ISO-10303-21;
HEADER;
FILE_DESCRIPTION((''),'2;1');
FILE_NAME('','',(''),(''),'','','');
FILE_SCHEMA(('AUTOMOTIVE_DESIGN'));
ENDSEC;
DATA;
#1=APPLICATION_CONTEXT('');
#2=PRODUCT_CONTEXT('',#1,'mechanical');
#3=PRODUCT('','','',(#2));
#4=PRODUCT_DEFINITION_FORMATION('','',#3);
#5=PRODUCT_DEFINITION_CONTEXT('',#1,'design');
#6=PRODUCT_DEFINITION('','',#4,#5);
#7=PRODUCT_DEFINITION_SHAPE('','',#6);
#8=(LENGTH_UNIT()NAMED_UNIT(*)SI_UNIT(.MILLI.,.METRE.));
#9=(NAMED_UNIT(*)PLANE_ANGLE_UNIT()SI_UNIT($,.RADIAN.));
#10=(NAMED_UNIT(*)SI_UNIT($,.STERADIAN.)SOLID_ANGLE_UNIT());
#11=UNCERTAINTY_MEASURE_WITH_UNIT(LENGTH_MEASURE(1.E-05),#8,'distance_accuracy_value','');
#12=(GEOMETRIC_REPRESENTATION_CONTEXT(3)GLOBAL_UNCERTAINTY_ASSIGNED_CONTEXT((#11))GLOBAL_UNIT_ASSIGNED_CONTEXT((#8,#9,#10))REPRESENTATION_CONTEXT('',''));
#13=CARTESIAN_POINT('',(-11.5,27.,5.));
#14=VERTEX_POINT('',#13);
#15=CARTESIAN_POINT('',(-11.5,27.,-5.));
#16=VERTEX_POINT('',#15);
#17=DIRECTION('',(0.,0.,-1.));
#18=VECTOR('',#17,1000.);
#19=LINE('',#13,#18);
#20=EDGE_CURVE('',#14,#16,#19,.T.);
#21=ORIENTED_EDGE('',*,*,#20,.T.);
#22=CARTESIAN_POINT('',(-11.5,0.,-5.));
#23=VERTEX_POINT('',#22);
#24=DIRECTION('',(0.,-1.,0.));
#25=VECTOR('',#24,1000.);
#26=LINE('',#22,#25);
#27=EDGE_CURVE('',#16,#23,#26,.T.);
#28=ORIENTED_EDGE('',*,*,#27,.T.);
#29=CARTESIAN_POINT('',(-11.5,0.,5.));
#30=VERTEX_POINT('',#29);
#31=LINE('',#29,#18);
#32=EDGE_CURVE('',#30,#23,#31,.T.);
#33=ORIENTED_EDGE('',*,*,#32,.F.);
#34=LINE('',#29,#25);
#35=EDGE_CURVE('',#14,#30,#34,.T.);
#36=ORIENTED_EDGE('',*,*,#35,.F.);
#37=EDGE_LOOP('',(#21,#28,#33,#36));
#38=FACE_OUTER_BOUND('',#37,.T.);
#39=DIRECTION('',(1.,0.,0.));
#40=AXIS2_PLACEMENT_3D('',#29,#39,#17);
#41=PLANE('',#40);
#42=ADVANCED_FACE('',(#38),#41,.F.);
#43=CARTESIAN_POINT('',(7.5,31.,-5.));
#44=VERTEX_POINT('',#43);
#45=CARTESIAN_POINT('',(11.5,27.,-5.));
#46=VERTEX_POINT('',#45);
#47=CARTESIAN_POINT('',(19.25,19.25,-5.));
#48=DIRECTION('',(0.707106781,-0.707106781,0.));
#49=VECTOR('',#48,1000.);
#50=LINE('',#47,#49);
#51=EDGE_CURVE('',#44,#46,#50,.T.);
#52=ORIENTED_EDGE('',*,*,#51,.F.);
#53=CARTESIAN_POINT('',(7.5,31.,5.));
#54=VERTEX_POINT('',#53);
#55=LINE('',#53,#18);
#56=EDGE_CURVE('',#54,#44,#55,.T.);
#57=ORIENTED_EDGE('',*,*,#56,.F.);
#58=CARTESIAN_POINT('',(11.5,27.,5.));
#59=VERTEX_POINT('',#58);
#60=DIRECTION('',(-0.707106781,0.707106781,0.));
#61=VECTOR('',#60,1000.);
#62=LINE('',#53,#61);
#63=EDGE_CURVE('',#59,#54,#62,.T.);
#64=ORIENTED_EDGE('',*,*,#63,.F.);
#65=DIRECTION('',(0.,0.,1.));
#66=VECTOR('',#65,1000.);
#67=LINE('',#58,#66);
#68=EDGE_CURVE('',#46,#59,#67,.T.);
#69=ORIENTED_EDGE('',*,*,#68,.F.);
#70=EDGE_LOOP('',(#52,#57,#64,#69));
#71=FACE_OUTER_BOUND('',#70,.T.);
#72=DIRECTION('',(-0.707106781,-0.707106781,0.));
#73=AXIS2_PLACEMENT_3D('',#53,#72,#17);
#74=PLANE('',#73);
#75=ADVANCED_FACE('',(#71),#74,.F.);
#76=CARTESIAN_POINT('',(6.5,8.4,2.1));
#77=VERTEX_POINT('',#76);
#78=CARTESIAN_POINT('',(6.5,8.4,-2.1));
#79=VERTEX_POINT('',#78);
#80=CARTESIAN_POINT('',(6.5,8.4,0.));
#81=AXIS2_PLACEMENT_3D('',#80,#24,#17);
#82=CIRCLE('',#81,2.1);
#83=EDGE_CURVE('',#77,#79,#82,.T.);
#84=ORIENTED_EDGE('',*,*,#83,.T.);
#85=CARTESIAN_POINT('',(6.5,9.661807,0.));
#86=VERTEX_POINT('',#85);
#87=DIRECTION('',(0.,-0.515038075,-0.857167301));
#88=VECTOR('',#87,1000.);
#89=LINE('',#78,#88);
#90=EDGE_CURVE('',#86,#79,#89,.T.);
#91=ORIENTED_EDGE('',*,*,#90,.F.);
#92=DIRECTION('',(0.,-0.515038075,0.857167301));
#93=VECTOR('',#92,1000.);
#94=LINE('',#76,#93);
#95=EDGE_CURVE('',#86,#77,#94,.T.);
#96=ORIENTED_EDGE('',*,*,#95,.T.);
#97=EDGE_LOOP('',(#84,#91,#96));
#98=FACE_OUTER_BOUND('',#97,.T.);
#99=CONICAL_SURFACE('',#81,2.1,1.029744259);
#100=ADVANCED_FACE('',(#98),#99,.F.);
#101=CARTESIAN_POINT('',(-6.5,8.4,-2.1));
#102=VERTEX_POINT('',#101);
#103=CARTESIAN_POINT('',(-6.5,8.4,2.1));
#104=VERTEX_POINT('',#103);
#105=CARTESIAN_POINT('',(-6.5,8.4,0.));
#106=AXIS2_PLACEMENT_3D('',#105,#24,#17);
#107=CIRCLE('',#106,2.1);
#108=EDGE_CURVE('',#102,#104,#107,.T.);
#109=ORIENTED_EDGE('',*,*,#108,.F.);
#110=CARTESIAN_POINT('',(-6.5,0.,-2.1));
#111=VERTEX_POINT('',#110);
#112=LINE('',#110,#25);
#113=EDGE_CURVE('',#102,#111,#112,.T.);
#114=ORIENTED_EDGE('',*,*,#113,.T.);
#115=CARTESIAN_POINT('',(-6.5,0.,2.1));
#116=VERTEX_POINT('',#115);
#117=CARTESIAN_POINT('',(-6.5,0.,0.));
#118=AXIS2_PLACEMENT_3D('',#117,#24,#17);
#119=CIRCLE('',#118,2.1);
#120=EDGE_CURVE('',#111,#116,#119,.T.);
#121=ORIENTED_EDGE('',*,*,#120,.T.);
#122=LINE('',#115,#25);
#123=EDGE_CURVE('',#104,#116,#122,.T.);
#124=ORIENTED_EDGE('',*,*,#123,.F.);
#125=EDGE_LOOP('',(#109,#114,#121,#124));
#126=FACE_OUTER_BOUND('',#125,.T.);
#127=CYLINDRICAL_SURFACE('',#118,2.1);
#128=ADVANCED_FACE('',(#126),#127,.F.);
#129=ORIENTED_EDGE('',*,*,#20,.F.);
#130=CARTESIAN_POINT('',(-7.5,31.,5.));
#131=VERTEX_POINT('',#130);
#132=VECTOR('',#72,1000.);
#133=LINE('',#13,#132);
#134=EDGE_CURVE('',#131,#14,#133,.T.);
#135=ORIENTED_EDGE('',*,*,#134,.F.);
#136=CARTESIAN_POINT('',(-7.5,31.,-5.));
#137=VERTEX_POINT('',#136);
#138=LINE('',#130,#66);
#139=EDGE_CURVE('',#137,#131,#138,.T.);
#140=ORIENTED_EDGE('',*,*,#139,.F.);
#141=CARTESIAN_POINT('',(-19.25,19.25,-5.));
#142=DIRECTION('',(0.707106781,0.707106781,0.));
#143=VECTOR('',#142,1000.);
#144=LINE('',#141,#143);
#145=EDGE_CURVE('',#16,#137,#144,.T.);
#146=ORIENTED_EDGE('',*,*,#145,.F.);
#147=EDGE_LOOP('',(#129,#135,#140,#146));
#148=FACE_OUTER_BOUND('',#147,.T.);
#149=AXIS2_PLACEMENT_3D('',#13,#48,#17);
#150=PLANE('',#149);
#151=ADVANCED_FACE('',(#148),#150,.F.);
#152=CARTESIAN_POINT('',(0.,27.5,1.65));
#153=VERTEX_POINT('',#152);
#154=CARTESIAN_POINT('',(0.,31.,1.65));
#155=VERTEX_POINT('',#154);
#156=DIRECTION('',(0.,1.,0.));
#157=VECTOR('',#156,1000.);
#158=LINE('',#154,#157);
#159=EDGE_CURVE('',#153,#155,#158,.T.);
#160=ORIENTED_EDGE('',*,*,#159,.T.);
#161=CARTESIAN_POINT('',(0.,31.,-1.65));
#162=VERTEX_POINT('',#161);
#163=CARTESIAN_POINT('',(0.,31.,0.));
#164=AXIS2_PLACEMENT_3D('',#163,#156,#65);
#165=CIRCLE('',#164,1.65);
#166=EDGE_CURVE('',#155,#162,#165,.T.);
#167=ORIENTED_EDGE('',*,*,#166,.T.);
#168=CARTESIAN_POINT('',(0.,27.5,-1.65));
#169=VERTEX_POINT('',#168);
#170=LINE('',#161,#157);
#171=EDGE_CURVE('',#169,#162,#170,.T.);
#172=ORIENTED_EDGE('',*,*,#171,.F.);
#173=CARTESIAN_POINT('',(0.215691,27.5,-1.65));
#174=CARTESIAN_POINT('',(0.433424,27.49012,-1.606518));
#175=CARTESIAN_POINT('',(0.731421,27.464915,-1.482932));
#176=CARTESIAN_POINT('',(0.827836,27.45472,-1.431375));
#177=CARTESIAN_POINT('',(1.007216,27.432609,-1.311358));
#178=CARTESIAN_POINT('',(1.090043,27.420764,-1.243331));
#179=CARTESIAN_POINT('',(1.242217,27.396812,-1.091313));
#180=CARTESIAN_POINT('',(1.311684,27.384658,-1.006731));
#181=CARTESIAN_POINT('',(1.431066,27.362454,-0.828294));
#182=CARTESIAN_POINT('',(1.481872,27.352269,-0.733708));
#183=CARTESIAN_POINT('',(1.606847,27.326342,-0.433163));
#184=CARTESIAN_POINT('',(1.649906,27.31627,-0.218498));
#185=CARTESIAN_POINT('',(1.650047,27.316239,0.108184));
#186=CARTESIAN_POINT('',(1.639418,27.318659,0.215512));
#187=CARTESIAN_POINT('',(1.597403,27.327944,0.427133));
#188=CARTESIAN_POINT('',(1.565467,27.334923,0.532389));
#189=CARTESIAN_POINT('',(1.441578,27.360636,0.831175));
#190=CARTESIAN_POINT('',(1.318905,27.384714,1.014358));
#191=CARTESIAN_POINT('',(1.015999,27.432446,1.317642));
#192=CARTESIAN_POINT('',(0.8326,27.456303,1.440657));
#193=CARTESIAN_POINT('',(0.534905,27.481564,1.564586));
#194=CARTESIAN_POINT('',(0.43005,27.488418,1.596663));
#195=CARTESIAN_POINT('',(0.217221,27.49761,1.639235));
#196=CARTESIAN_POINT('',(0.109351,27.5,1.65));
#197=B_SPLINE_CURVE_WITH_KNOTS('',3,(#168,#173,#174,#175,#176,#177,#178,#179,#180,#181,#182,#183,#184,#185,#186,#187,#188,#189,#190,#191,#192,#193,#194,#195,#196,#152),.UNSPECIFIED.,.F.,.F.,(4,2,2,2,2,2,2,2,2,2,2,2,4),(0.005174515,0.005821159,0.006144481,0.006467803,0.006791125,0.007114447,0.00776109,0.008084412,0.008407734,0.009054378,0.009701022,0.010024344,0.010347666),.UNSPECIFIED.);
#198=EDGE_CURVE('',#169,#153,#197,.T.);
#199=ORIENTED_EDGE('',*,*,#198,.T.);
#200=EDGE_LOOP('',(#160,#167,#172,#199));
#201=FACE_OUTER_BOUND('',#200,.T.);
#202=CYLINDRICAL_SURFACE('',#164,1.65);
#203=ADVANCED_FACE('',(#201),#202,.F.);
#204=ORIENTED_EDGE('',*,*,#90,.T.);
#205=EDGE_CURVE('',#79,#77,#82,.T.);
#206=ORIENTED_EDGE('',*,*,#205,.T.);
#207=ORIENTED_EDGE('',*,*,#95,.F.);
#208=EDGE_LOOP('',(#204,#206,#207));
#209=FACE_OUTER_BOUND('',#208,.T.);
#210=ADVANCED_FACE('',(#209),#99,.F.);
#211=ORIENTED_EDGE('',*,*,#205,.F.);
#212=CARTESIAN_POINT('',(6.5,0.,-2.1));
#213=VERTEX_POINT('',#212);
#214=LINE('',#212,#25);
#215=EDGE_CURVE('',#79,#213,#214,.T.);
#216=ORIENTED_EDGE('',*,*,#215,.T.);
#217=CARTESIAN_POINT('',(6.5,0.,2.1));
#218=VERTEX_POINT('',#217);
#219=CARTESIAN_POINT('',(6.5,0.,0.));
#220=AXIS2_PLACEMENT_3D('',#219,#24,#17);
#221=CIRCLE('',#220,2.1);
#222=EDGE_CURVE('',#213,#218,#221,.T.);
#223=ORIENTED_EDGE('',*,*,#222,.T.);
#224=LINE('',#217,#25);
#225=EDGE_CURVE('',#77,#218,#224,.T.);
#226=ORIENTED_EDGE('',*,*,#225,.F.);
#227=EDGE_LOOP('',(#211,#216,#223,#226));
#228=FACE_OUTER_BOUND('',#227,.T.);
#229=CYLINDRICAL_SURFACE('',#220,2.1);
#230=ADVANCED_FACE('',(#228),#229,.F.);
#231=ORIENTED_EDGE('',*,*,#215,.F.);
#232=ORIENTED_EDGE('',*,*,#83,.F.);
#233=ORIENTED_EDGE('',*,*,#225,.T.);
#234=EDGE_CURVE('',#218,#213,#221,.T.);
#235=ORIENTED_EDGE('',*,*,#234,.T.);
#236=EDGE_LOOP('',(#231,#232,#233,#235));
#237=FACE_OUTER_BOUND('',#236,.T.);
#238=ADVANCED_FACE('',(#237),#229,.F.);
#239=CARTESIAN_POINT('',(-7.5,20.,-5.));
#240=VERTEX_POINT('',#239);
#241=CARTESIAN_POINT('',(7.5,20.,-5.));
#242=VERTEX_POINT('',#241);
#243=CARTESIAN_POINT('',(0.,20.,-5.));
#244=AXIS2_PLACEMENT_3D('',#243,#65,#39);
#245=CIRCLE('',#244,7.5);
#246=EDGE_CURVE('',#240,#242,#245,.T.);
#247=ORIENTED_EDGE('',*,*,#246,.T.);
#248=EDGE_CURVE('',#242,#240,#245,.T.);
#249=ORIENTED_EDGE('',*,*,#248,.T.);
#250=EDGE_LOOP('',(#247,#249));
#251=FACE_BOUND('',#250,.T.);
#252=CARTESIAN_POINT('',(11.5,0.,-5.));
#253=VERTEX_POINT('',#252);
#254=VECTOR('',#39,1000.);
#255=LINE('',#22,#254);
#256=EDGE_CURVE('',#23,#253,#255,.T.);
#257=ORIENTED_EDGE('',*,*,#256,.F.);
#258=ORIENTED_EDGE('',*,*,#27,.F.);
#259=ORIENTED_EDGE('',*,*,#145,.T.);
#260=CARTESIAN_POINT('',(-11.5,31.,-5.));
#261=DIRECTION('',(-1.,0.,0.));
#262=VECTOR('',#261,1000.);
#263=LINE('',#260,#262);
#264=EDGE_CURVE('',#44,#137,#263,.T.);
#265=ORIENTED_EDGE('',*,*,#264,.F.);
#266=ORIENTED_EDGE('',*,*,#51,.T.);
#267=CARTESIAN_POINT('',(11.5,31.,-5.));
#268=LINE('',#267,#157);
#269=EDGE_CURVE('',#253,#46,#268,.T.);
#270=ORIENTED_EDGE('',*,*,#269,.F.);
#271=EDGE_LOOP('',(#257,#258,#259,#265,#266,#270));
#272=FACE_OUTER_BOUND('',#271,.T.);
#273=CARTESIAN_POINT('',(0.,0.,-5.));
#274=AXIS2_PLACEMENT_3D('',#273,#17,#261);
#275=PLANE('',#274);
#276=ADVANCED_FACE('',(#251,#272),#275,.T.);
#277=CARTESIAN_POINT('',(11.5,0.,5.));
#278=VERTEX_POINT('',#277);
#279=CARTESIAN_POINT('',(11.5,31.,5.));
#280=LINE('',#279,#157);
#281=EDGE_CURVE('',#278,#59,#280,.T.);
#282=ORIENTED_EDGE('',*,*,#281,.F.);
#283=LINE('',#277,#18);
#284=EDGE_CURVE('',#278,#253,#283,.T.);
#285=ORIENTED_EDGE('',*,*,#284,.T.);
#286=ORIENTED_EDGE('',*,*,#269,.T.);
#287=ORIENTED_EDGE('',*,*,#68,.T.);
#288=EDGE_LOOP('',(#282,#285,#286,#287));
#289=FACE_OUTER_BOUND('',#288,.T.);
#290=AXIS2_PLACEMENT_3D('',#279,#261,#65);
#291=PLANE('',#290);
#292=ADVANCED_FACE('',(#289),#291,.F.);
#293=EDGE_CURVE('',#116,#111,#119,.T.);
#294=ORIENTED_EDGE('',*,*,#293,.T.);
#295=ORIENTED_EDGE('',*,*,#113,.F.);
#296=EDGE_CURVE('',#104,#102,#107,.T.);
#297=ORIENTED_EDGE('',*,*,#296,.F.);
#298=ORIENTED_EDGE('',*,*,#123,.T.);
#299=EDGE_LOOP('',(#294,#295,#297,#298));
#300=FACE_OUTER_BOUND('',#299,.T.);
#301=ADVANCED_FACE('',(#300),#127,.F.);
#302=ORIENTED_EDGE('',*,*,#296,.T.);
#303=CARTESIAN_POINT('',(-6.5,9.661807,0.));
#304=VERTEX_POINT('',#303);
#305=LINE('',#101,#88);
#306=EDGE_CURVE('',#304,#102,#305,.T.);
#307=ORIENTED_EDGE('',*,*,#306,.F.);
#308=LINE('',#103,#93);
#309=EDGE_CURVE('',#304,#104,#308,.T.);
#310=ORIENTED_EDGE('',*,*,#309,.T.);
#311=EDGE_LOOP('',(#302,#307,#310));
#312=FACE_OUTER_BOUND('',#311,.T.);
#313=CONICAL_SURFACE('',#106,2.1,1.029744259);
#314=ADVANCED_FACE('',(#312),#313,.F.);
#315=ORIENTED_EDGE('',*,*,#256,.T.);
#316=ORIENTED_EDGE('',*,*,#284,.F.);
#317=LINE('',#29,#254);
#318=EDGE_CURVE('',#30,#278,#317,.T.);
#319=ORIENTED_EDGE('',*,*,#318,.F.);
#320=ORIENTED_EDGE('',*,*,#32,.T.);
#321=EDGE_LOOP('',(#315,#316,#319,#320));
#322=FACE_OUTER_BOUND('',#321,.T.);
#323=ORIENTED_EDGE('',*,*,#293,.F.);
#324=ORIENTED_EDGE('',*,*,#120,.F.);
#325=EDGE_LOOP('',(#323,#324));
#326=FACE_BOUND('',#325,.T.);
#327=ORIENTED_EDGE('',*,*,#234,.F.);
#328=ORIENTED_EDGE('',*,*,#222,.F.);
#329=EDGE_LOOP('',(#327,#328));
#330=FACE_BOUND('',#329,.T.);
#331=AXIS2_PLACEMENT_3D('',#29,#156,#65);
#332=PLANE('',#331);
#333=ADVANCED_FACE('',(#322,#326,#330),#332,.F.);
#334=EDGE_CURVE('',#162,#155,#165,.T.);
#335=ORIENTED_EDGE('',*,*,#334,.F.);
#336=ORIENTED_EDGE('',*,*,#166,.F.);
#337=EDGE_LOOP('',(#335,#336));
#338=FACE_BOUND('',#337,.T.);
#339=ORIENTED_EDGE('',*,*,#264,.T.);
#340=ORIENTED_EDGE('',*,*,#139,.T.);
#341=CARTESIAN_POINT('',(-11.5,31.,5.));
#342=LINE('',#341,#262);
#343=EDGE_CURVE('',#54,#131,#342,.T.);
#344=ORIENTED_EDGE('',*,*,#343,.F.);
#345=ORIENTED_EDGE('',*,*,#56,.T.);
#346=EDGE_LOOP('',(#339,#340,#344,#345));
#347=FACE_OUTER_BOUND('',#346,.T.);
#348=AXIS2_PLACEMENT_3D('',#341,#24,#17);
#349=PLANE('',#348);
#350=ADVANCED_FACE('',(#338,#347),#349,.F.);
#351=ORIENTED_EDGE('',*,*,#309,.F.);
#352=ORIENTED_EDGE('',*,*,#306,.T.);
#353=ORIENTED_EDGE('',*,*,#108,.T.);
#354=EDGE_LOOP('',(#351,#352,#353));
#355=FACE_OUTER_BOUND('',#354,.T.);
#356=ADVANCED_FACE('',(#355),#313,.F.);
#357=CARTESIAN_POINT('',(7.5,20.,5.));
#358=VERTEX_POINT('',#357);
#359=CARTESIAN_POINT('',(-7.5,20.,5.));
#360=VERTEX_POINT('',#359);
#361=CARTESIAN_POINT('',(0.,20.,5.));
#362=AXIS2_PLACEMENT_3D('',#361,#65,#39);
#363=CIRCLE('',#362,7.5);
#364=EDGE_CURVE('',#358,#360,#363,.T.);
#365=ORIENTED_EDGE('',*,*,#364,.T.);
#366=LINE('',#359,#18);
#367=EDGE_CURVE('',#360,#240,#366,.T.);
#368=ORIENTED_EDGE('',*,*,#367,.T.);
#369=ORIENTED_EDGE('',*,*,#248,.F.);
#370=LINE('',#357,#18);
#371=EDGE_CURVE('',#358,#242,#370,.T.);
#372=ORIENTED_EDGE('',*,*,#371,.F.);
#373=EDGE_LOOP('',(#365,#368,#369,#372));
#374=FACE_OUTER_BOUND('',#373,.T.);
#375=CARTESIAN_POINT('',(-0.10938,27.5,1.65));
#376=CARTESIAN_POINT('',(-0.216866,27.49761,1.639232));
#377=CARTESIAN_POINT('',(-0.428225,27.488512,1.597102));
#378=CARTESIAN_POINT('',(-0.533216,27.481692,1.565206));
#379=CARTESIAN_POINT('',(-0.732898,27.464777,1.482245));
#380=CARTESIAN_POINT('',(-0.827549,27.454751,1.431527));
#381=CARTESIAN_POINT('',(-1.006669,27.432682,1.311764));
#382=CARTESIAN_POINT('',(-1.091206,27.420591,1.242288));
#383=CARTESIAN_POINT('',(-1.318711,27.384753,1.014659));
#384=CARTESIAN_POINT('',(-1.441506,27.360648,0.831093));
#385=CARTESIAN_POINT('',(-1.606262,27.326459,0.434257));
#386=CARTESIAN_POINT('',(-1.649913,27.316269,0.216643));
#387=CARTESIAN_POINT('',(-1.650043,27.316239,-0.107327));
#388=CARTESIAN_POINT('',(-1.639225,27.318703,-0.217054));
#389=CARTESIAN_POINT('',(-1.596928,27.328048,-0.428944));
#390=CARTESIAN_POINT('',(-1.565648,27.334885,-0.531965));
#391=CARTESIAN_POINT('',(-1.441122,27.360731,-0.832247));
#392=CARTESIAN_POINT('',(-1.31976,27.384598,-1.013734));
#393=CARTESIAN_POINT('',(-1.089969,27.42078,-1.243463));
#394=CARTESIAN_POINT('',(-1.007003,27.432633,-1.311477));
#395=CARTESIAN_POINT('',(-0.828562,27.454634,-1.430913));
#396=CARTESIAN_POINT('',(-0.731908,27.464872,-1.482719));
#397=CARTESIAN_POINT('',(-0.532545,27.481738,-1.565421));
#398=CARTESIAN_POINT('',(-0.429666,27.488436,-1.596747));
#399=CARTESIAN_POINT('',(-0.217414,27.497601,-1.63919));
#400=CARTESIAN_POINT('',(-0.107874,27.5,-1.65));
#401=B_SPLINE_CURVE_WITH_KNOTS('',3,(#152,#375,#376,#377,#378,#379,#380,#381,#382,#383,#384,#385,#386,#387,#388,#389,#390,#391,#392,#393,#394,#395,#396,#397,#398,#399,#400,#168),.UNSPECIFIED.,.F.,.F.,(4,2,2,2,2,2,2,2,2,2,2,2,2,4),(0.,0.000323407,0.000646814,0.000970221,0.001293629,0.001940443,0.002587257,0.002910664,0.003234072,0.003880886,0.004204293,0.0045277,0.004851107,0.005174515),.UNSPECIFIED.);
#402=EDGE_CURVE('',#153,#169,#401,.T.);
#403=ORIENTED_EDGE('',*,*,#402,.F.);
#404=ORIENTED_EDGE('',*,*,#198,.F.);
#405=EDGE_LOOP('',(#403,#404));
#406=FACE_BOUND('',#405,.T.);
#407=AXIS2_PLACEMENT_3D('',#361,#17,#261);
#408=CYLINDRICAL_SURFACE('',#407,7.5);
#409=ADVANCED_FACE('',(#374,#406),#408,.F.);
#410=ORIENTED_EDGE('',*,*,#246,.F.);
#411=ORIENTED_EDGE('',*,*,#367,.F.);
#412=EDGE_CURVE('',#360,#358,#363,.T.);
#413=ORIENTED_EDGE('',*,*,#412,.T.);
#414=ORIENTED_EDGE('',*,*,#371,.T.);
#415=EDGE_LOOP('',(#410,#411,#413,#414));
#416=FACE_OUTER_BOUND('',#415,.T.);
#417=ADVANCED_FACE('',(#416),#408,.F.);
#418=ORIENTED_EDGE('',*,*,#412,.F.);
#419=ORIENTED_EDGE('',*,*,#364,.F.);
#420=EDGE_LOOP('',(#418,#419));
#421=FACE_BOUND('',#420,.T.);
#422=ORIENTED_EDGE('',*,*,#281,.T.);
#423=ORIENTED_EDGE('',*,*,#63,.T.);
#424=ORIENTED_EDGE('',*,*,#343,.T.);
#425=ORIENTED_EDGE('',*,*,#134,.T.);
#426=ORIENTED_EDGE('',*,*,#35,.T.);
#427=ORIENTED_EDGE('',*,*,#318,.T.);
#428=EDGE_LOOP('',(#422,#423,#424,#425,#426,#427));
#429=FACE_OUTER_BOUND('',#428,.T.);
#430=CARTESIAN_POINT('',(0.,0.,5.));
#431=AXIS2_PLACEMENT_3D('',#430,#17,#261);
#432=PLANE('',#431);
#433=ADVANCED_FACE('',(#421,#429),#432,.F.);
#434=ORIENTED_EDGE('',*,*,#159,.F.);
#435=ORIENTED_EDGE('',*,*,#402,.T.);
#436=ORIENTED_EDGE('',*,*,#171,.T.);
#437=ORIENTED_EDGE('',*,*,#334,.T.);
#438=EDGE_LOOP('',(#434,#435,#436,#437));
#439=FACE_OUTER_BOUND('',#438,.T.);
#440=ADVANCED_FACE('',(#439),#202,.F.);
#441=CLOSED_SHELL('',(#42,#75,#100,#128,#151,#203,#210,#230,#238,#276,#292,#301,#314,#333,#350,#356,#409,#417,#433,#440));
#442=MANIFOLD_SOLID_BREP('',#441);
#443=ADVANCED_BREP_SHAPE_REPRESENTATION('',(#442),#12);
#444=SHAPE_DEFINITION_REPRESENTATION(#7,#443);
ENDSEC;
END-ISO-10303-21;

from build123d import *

# Parameters (mm, degrees)
SKETCH_1_W              = 23
SKETCH_1_H              = 31
SKETCH_1_R              = 7.5
EXTRUDE_1_DEPTH         = 5
CHAMFER_1_SIZE          = 4
HOLE_WIZARD_M4_1_REACH  = 35.44
HOLE_WIZARD_M4_1_BORE_R = 1.65
HOLE_WIZARD_M5_2_D      = 4.2
HOLE_WIZARD_M5_2_DEPTH  = 8.4
HOLE_WIZARD_M5_2_TIP    = 1.2618073


with BuildPart() as part:
    # 草图1 → 凸台-拉伸1 (new, symmetric)
    with BuildSketch(Plane.XY):
        with Locations((0, 15.5)):
            Rectangle(SKETCH_1_W, SKETCH_1_H)
        with Locations((0, 20)):
            Circle(SKETCH_1_R, mode=Mode.SUBTRACT)
    extrude(amount=EXTRUDE_1_DEPTH, both=True)

    # 倒角1
    chamfer_1_edges = [part.edges().sort_by_distance(p)[0] for p in [
        (11.5, 31, 0),
        (-11.5, 31, 0),
    ]]
    chamfer(chamfer_1_edges, length=CHAMFER_1_SIZE)

    # M4 螺纹孔1 bore (on position points) → M4 螺纹孔1 (cut, up to next)
    with BuildSketch(Plane.ZX.offset(31), mode=Mode.PRIVATE) as hole_wizard_m4_1_sk1:
        Circle(HOLE_WIZARD_M4_1_BORE_R)
    hole_wizard_m4_1_tool1 = extrude(hole_wizard_m4_1_sk1.sketch, amount=-HOLE_WIZARD_M4_1_REACH, mode=Mode.PRIVATE) & part.part
    add(hole_wizard_m4_1_tool1.solids().sort_by_distance((0, 31, 0))[0], mode=Mode.SUBTRACT)

    # M5 螺纹孔2
    with Locations(Plane(origin=(-6.5, 0, 0), x_dir=(0, 0, -1), z_dir=(0, -1, 0))):
        with Locations((0, 0), (0, 13)):
            Hole(HOLE_WIZARD_M5_2_D / 2, depth=HOLE_WIZARD_M5_2_DEPTH)
            with Locations((0, 0, -(HOLE_WIZARD_M5_2_DEPTH + HOLE_WIZARD_M5_2_TIP / 2))):  # 118° drill point
                Cone(0, HOLE_WIZARD_M5_2_D / 2, HOLE_WIZARD_M5_2_TIP, mode=Mode.SUBTRACT)


solid = part.part
